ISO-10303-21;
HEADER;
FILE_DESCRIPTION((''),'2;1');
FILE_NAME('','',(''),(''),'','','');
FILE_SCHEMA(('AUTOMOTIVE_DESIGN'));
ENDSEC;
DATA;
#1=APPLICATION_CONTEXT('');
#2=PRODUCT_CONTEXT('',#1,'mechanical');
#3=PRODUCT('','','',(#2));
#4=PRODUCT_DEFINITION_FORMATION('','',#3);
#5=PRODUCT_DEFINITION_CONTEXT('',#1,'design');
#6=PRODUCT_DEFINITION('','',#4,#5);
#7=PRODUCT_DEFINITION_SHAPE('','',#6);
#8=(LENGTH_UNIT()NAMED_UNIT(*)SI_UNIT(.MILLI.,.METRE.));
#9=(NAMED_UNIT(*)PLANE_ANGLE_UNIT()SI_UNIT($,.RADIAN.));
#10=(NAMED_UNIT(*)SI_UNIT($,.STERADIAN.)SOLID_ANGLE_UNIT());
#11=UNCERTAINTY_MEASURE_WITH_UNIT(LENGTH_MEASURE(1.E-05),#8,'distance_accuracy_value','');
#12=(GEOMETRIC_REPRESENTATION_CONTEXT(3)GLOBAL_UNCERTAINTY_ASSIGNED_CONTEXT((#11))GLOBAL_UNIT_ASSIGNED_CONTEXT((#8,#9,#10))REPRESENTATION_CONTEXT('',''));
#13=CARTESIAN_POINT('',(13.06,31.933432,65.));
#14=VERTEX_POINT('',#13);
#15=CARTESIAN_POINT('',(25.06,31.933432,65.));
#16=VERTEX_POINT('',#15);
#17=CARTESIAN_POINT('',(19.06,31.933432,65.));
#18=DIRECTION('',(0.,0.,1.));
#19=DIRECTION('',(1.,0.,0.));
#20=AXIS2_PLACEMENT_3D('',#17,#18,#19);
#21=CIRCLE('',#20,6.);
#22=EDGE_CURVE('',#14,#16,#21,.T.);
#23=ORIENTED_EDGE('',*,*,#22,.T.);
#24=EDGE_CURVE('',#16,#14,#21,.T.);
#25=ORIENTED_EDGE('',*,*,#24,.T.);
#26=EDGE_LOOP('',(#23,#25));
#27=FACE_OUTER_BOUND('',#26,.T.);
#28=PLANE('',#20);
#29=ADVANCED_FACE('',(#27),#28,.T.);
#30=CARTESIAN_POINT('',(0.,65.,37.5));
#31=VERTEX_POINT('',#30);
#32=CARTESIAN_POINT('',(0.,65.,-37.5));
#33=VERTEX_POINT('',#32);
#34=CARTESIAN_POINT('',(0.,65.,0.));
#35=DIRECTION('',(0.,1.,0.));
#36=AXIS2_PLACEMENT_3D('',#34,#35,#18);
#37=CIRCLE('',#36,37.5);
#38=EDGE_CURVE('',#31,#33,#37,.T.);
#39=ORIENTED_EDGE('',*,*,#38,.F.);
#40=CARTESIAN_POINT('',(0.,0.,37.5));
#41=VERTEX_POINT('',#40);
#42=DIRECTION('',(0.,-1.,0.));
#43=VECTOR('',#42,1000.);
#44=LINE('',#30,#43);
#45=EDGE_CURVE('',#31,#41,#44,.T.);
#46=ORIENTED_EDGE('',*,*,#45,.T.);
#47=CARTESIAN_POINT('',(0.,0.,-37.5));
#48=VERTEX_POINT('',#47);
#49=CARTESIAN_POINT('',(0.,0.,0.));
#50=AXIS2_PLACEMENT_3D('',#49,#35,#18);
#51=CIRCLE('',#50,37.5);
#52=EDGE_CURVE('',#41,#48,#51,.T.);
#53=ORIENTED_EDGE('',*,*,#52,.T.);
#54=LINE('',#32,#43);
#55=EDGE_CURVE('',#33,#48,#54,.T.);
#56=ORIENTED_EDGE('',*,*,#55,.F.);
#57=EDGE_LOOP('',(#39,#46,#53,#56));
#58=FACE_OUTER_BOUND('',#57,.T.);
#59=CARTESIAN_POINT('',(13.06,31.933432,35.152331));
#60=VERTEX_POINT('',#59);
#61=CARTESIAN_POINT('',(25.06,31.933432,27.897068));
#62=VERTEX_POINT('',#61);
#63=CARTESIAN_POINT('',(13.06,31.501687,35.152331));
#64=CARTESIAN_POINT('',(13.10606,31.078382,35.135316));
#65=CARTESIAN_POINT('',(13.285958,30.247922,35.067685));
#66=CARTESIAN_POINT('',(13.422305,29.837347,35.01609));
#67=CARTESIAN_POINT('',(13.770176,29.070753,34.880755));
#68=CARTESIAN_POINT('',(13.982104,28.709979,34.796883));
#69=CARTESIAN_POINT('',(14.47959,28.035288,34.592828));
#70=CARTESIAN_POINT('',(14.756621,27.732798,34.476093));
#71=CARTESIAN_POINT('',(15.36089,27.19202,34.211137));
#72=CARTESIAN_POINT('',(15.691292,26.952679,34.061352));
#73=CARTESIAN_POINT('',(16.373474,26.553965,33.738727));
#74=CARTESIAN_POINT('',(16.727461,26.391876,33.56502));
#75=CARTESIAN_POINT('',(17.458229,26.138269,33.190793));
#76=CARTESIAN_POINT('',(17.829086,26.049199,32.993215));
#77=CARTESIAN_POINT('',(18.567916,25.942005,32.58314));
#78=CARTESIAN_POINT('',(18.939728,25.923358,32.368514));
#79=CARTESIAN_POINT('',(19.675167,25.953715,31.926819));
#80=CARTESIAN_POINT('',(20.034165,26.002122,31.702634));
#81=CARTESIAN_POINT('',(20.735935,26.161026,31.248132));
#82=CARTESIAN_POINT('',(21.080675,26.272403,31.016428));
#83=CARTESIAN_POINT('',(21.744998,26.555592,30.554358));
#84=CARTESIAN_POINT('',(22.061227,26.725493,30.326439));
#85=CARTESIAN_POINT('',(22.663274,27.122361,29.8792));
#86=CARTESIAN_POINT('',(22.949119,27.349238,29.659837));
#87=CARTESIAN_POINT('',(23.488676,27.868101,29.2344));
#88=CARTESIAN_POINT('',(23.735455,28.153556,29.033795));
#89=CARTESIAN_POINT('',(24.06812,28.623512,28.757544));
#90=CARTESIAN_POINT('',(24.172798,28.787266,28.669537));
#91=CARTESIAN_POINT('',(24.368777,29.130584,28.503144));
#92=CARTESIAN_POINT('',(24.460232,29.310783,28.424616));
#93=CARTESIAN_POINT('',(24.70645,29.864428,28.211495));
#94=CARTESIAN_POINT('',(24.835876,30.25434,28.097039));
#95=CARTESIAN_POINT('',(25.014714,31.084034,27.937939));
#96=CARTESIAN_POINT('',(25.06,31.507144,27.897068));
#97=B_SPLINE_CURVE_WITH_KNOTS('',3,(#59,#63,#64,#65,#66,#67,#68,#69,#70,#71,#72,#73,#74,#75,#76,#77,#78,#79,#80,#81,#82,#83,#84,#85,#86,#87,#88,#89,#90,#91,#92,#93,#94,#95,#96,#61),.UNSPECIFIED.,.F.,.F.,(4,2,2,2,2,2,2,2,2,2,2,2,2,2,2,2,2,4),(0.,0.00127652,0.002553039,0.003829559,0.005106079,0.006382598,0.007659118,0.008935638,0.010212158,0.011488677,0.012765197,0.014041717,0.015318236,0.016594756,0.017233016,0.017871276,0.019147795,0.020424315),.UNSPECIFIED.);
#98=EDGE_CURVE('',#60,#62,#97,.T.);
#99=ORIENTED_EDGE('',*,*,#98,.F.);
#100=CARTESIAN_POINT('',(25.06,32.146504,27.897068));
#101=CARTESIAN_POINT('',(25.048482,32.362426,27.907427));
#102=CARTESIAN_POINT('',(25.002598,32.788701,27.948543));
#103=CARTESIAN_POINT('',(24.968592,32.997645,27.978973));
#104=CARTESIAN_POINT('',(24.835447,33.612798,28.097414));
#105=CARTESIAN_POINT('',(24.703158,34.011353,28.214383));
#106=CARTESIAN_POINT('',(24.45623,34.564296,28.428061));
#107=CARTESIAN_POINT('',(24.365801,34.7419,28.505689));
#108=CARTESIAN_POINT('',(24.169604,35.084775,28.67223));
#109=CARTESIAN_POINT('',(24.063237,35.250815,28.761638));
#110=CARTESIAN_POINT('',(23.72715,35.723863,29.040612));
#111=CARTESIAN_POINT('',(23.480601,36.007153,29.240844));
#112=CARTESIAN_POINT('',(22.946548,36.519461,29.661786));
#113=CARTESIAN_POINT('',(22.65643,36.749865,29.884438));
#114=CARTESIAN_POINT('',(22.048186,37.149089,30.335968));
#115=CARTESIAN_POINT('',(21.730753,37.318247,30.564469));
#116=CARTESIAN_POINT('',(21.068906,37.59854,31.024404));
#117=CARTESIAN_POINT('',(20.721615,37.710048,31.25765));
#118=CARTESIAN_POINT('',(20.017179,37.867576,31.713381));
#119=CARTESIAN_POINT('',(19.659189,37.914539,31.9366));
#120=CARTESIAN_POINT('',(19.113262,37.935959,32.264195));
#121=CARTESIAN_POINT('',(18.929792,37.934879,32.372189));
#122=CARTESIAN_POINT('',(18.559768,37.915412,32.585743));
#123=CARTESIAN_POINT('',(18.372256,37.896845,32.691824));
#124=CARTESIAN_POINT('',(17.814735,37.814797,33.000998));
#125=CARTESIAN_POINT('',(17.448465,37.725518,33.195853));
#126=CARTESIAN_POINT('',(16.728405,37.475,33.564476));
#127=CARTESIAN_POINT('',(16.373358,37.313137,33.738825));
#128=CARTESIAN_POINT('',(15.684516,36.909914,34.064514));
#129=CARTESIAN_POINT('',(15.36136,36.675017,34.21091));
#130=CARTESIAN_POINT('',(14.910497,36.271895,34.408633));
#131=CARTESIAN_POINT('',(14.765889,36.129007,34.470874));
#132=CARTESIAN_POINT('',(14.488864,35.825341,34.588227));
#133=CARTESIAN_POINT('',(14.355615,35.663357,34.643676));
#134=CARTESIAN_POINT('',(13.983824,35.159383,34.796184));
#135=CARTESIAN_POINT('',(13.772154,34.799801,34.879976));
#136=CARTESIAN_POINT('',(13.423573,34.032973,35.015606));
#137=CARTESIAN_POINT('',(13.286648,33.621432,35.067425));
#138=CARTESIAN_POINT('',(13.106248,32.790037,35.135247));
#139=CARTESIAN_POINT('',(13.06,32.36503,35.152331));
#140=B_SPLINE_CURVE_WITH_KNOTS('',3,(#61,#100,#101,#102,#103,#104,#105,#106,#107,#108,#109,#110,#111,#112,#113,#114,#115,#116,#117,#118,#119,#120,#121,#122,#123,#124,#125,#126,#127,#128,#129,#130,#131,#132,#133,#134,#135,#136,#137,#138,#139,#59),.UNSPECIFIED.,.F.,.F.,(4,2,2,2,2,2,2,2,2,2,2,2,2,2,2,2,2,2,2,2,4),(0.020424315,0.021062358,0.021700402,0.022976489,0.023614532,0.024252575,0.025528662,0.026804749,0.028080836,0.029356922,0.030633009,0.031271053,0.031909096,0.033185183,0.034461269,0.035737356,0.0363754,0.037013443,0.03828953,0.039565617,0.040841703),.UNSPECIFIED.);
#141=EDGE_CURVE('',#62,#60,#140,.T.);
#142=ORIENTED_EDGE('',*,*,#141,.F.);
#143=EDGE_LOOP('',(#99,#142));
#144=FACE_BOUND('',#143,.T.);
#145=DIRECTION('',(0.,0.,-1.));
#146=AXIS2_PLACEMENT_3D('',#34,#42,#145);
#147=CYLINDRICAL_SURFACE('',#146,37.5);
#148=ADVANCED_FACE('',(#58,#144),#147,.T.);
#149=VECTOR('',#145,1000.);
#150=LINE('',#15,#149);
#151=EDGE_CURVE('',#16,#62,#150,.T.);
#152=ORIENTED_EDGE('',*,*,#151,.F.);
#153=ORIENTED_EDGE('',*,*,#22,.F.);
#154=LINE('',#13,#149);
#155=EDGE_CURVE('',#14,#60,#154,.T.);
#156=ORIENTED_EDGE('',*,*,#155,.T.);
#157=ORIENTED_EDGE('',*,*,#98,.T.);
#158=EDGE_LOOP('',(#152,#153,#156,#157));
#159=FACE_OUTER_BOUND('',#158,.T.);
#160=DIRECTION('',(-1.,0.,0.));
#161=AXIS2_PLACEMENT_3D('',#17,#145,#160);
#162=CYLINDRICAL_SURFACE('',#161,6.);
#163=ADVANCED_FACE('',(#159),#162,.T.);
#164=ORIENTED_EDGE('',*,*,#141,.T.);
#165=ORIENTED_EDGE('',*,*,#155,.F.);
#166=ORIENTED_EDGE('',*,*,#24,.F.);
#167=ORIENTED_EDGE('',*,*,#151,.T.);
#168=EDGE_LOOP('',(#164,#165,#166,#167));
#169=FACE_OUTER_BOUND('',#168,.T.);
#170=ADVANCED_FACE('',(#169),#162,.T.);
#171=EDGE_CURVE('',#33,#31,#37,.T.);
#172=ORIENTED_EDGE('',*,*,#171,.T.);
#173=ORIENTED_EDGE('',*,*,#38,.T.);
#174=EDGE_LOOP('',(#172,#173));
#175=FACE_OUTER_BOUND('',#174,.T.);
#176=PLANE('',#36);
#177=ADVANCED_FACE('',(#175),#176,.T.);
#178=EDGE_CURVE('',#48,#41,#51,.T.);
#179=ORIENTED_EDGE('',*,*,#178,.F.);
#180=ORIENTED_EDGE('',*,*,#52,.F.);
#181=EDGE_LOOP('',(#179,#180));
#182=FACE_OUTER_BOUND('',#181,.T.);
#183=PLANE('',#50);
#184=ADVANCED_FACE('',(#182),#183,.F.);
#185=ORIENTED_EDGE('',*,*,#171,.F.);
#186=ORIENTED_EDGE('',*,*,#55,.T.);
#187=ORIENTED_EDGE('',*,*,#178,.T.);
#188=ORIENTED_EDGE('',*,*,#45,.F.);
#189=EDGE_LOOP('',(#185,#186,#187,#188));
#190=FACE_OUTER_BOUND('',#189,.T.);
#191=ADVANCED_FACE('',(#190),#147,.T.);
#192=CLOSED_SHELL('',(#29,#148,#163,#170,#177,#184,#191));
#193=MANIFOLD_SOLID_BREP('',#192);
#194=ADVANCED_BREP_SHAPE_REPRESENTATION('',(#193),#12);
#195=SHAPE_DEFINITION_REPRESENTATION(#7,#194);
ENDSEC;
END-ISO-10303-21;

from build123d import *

# Parameters (mm, degrees)
SKETCH1_R           = 37.5
BOSS_EXTRUDE1_DEPTH = 65
SKETCH2_R           = 6
BOSS_EXTRUDE2_DEPTH = 65


with BuildPart() as part:
    # Sketch1 → Boss-Extrude1 (new body)
    with BuildSketch(Plane(origin=(0, 0, 0), x_dir=(1, 0, 0), z_dir=(0, 1, 0))):
        with Locations(Location((0, 0, 0), (0, 0, 270))):
            Circle(SKETCH1_R)
    extrude(amount=BOSS_EXTRUDE1_DEPTH)

    # Sketch2 → Boss-Extrude2 (add)
    with BuildSketch(Plane.XY):
        with Locations(Location((19.06, 31.933431832, 0), (0, 0, 180))):
            Circle(SKETCH2_R)
    extrude(amount=BOSS_EXTRUDE2_DEPTH)


solid = part.part
